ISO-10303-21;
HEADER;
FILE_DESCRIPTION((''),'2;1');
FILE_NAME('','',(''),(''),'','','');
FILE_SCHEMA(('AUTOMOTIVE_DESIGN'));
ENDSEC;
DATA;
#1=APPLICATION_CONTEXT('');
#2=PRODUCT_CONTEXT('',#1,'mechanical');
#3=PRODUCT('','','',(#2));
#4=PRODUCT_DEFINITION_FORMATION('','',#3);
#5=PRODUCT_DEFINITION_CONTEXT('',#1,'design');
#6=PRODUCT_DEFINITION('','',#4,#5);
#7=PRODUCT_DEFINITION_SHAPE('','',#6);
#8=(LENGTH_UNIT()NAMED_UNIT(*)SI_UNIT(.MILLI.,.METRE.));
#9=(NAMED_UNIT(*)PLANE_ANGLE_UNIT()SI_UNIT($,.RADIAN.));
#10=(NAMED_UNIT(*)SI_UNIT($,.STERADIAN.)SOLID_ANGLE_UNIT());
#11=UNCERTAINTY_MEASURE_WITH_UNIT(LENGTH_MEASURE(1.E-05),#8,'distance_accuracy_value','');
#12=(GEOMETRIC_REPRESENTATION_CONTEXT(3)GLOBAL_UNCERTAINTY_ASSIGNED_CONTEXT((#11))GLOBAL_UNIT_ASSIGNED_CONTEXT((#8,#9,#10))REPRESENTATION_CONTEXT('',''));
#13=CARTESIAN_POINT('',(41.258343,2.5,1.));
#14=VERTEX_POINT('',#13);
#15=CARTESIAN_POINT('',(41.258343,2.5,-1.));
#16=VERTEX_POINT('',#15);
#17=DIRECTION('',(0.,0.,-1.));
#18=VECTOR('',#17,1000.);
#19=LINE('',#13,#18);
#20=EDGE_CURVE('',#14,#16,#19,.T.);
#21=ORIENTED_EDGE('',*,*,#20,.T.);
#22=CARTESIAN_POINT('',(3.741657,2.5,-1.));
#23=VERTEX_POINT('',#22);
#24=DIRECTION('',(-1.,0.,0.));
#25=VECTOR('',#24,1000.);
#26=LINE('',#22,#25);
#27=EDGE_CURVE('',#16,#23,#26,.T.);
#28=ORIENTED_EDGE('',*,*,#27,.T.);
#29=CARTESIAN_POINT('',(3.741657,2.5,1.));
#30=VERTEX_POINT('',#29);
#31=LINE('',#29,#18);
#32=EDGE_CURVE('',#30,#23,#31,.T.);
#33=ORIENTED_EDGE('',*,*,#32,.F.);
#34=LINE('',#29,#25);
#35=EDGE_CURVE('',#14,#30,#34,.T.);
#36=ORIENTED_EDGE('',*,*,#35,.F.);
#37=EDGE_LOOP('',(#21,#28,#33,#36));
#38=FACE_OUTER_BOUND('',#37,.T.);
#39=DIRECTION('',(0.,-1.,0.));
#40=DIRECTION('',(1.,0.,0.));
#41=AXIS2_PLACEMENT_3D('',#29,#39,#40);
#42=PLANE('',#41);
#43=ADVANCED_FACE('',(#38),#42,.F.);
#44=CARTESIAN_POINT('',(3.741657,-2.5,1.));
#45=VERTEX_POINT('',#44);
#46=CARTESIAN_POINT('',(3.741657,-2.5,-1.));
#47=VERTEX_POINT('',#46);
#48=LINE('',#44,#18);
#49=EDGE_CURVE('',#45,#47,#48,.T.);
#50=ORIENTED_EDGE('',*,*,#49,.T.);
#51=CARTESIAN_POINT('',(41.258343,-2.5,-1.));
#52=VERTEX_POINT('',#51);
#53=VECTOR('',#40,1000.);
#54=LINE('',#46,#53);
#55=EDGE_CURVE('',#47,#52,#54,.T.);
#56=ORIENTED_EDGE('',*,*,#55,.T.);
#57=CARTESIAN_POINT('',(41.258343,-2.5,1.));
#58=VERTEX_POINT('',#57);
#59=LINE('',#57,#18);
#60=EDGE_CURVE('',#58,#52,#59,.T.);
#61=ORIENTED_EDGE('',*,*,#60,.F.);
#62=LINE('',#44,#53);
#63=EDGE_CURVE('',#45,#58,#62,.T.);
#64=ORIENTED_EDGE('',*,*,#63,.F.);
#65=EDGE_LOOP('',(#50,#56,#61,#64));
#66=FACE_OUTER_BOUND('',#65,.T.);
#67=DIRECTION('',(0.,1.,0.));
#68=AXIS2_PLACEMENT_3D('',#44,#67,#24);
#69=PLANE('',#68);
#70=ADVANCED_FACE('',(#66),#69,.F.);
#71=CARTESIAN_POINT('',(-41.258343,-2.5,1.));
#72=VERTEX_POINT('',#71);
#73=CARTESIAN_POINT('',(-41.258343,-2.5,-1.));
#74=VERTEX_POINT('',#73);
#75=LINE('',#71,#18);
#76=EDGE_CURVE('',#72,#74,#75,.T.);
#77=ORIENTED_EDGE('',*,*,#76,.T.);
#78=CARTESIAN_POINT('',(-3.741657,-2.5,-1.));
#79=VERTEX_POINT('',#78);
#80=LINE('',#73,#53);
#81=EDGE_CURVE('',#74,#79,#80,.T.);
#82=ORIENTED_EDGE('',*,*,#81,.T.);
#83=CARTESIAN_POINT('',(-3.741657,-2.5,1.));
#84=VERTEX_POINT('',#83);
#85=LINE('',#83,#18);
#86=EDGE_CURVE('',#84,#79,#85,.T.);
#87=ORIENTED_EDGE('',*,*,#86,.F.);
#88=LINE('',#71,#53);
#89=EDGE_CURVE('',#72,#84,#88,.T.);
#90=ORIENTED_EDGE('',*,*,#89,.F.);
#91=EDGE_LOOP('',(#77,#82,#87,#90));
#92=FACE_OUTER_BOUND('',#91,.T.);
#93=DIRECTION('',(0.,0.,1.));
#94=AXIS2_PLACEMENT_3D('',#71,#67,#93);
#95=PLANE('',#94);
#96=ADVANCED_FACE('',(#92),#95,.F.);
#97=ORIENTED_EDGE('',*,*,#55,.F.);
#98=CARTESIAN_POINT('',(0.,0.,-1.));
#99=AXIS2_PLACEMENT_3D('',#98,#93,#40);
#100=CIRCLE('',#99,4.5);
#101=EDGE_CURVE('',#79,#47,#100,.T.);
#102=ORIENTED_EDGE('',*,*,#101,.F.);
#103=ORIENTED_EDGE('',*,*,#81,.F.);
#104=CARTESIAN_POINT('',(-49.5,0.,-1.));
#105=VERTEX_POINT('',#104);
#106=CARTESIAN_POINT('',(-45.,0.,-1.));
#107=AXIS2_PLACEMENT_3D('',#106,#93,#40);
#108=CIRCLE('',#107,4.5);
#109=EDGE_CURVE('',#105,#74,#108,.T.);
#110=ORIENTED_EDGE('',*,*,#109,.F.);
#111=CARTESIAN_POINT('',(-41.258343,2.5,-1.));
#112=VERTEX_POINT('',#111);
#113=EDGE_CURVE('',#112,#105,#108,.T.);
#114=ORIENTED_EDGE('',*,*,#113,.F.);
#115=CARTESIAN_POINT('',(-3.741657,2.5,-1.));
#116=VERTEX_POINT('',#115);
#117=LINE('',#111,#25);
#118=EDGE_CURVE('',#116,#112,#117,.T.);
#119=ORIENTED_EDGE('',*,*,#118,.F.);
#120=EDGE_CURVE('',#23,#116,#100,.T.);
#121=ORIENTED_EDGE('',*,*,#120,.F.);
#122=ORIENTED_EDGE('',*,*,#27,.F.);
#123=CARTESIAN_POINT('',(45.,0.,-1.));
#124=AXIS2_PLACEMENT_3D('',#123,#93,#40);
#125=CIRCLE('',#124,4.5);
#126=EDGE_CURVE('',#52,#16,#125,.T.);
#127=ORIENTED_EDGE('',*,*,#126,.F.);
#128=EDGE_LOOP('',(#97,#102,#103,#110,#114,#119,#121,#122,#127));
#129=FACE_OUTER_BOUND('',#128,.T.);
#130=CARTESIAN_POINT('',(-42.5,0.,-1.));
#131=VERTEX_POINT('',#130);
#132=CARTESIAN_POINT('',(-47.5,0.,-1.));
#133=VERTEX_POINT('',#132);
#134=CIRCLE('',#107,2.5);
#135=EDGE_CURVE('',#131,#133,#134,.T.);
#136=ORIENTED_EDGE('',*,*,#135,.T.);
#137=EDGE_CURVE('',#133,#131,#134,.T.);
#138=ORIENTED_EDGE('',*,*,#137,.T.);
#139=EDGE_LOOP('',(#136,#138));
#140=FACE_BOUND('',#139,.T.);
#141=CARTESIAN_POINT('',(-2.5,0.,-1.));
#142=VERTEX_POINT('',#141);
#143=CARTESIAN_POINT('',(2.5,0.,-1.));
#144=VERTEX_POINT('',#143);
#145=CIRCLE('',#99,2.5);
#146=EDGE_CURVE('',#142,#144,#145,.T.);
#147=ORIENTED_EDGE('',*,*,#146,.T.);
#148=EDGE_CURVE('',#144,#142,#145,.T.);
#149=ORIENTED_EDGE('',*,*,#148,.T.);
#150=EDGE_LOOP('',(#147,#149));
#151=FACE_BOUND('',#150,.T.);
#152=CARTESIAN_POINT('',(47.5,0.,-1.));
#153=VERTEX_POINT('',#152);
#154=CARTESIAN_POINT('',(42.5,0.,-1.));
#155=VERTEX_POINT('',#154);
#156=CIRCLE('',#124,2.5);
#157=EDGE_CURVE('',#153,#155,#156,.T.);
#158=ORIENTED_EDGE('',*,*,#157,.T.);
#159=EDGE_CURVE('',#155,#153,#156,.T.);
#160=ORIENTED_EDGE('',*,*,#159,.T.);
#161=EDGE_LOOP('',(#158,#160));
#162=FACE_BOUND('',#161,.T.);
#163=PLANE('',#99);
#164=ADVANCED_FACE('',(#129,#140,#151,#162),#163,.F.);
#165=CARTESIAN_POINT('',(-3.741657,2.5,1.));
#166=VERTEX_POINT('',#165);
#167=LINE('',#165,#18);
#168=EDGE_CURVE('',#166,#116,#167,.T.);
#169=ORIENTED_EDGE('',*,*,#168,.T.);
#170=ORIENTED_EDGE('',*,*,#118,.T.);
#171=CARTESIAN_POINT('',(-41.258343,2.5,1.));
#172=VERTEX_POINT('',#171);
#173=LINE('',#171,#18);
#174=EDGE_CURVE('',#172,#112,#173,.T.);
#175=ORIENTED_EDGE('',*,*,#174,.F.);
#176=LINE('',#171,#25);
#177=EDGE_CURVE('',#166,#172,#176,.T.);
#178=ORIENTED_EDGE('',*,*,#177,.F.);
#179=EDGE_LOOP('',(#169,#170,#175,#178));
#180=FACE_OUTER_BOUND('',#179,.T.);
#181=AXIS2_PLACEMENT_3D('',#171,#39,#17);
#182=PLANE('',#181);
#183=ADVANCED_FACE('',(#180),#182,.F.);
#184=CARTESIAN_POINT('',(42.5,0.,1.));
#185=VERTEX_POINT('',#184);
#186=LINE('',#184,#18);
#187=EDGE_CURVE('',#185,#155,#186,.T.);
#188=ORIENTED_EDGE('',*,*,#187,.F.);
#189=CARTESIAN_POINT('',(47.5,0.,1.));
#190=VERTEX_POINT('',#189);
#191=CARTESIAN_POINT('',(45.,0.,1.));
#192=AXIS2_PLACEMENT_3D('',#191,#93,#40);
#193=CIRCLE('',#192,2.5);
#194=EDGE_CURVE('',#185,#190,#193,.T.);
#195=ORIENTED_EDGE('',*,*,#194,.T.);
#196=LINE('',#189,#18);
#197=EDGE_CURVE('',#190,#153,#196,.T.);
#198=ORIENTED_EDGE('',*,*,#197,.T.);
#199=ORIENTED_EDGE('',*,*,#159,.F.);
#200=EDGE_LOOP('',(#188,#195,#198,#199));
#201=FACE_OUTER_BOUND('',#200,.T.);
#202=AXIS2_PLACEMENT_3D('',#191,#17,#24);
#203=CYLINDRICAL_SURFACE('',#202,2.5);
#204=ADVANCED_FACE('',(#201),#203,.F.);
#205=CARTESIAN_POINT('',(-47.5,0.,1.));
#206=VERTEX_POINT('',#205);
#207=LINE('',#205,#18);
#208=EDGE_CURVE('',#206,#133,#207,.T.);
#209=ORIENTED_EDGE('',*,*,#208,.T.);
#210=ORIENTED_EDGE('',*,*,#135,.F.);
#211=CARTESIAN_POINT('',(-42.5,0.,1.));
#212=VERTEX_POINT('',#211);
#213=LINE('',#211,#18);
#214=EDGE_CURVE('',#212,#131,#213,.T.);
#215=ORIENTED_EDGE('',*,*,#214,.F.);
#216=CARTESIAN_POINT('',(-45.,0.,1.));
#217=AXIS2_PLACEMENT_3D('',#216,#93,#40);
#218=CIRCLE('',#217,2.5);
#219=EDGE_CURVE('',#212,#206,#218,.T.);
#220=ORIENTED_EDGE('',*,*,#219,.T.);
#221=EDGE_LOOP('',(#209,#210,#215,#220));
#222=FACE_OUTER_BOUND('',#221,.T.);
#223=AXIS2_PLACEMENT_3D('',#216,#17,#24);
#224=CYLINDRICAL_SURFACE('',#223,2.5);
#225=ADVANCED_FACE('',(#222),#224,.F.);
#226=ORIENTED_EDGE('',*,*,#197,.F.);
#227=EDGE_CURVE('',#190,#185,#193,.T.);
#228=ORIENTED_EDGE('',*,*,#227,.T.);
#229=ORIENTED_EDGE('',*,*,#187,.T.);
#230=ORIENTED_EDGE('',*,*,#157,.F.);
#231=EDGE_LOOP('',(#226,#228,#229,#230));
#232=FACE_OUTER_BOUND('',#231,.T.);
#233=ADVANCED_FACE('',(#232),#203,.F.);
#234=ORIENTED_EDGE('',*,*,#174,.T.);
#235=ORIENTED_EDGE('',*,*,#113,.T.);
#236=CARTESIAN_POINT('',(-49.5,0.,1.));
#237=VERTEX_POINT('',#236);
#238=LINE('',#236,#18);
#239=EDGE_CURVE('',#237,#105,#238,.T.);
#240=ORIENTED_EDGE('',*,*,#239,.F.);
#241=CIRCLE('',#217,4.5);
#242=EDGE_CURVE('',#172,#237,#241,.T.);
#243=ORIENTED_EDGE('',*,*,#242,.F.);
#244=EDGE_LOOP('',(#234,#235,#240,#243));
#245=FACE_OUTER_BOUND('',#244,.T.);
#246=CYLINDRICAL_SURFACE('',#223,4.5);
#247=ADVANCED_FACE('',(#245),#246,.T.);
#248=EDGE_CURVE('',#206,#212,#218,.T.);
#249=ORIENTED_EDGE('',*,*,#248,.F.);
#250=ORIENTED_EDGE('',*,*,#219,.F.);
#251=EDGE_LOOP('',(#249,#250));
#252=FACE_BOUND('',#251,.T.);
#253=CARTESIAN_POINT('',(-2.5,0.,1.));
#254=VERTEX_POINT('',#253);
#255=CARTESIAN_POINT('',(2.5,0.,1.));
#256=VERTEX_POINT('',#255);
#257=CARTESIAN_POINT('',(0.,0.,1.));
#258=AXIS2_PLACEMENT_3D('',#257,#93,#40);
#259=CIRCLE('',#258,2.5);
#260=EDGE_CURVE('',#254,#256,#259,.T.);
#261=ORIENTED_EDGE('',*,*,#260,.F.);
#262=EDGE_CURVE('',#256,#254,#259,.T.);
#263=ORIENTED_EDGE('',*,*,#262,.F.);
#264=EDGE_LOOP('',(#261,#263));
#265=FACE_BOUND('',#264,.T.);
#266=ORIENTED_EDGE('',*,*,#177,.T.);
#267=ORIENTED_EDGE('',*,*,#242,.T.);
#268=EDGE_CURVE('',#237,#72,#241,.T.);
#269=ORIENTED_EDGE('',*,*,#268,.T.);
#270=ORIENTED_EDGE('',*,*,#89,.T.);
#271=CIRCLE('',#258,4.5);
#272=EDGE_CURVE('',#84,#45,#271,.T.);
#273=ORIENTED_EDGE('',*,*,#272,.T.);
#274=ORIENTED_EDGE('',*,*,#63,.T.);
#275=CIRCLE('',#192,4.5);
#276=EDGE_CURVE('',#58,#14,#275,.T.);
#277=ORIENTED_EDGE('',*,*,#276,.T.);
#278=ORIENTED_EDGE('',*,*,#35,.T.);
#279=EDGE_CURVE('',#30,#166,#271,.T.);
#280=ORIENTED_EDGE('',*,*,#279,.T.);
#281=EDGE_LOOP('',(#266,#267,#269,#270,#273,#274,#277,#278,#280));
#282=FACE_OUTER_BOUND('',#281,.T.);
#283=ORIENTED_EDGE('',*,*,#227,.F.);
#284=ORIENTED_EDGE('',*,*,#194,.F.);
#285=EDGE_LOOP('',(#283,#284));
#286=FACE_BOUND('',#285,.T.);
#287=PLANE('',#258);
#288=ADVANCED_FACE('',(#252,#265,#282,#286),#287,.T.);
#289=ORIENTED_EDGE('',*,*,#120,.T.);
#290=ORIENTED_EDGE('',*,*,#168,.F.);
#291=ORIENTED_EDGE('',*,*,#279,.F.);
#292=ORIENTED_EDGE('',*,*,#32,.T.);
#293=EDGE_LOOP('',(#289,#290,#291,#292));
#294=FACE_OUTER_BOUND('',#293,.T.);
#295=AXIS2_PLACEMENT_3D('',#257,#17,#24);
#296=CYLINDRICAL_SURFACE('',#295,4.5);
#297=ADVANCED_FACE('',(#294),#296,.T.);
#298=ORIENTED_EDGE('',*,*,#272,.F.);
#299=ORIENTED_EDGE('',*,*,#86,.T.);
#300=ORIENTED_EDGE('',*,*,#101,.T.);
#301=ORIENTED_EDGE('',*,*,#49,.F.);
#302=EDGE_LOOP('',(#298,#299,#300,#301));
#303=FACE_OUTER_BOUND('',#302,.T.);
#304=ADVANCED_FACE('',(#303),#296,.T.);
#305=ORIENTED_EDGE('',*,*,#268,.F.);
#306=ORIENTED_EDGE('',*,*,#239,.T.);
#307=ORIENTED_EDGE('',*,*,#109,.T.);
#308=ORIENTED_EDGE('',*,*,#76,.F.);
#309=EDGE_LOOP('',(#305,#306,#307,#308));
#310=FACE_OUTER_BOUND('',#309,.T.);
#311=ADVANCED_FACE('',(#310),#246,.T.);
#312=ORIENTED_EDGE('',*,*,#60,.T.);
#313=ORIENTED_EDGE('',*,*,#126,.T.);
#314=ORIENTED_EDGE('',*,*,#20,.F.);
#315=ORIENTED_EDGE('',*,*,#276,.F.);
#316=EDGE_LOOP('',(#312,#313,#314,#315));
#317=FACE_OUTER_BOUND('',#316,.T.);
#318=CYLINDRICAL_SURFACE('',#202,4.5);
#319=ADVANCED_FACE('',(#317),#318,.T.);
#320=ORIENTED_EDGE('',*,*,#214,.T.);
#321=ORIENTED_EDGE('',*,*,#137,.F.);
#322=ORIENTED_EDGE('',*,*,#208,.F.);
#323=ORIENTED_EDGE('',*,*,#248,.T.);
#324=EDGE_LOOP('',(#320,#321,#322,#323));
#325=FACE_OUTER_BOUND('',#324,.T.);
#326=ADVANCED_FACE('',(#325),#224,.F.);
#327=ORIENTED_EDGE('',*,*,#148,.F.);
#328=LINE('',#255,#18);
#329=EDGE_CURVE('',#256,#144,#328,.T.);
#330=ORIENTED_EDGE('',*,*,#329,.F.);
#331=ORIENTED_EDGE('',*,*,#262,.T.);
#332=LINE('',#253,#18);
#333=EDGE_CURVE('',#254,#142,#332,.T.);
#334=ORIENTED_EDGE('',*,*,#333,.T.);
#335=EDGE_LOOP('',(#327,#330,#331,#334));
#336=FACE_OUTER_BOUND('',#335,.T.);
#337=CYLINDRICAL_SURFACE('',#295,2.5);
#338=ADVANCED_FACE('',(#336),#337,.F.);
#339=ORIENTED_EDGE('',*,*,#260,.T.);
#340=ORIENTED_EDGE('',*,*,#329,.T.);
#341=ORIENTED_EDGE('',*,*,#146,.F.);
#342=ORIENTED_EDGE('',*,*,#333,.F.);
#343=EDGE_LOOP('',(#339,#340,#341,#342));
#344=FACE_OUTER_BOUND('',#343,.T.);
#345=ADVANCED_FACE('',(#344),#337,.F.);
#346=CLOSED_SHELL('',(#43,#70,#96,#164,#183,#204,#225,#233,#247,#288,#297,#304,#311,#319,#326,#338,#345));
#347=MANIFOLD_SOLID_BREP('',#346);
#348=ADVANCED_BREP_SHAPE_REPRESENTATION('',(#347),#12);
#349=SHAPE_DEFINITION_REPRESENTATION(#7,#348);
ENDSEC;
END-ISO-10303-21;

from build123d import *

# Parameters (mm, degrees)
LINK_PROFILE_SKETCH_R = 2.5
LINK_PLATE_2MM_DEPTH  = 1


with BuildPart() as part:
    # Link Profile Sketch → Link Plate 2mm (new, symmetric)
    with BuildSketch(Plane.XY):
        with BuildLine():
            Line((3.741657387, 2.5), (41.258342613, 2.5))
            ThreePointArc((41.258342613, 2.5), (49.5, 0), (41.258342613, -2.5))
            Line((41.258342613, -2.5), (3.741657387, -2.5))
            ThreePointArc((3.741657387, -2.5), (0, -4.5), (-3.741657387, -2.5))
            Line((-3.741657387, -2.5), (-41.258342613, -2.5))
            ThreePointArc((-41.258342613, -2.5), (-49.5, 0), (-41.258342613, 2.5))
            Line((-41.258342613, 2.5), (-3.741657387, 2.5))
            ThreePointArc((-3.741657387, 2.5), (0, 4.5), (3.741657387, 2.5))
        make_face()
        with Locations((-45, 0)):
            Circle(LINK_PROFILE_SKETCH_R, mode=Mode.SUBTRACT)
        Circle(LINK_PROFILE_SKETCH_R, mode=Mode.SUBTRACT)
        with Locations((45, 0)):
            Circle(LINK_PROFILE_SKETCH_R, mode=Mode.SUBTRACT)
    extrude(amount=LINK_PLATE_2MM_DEPTH, both=True)


solid = part.part
